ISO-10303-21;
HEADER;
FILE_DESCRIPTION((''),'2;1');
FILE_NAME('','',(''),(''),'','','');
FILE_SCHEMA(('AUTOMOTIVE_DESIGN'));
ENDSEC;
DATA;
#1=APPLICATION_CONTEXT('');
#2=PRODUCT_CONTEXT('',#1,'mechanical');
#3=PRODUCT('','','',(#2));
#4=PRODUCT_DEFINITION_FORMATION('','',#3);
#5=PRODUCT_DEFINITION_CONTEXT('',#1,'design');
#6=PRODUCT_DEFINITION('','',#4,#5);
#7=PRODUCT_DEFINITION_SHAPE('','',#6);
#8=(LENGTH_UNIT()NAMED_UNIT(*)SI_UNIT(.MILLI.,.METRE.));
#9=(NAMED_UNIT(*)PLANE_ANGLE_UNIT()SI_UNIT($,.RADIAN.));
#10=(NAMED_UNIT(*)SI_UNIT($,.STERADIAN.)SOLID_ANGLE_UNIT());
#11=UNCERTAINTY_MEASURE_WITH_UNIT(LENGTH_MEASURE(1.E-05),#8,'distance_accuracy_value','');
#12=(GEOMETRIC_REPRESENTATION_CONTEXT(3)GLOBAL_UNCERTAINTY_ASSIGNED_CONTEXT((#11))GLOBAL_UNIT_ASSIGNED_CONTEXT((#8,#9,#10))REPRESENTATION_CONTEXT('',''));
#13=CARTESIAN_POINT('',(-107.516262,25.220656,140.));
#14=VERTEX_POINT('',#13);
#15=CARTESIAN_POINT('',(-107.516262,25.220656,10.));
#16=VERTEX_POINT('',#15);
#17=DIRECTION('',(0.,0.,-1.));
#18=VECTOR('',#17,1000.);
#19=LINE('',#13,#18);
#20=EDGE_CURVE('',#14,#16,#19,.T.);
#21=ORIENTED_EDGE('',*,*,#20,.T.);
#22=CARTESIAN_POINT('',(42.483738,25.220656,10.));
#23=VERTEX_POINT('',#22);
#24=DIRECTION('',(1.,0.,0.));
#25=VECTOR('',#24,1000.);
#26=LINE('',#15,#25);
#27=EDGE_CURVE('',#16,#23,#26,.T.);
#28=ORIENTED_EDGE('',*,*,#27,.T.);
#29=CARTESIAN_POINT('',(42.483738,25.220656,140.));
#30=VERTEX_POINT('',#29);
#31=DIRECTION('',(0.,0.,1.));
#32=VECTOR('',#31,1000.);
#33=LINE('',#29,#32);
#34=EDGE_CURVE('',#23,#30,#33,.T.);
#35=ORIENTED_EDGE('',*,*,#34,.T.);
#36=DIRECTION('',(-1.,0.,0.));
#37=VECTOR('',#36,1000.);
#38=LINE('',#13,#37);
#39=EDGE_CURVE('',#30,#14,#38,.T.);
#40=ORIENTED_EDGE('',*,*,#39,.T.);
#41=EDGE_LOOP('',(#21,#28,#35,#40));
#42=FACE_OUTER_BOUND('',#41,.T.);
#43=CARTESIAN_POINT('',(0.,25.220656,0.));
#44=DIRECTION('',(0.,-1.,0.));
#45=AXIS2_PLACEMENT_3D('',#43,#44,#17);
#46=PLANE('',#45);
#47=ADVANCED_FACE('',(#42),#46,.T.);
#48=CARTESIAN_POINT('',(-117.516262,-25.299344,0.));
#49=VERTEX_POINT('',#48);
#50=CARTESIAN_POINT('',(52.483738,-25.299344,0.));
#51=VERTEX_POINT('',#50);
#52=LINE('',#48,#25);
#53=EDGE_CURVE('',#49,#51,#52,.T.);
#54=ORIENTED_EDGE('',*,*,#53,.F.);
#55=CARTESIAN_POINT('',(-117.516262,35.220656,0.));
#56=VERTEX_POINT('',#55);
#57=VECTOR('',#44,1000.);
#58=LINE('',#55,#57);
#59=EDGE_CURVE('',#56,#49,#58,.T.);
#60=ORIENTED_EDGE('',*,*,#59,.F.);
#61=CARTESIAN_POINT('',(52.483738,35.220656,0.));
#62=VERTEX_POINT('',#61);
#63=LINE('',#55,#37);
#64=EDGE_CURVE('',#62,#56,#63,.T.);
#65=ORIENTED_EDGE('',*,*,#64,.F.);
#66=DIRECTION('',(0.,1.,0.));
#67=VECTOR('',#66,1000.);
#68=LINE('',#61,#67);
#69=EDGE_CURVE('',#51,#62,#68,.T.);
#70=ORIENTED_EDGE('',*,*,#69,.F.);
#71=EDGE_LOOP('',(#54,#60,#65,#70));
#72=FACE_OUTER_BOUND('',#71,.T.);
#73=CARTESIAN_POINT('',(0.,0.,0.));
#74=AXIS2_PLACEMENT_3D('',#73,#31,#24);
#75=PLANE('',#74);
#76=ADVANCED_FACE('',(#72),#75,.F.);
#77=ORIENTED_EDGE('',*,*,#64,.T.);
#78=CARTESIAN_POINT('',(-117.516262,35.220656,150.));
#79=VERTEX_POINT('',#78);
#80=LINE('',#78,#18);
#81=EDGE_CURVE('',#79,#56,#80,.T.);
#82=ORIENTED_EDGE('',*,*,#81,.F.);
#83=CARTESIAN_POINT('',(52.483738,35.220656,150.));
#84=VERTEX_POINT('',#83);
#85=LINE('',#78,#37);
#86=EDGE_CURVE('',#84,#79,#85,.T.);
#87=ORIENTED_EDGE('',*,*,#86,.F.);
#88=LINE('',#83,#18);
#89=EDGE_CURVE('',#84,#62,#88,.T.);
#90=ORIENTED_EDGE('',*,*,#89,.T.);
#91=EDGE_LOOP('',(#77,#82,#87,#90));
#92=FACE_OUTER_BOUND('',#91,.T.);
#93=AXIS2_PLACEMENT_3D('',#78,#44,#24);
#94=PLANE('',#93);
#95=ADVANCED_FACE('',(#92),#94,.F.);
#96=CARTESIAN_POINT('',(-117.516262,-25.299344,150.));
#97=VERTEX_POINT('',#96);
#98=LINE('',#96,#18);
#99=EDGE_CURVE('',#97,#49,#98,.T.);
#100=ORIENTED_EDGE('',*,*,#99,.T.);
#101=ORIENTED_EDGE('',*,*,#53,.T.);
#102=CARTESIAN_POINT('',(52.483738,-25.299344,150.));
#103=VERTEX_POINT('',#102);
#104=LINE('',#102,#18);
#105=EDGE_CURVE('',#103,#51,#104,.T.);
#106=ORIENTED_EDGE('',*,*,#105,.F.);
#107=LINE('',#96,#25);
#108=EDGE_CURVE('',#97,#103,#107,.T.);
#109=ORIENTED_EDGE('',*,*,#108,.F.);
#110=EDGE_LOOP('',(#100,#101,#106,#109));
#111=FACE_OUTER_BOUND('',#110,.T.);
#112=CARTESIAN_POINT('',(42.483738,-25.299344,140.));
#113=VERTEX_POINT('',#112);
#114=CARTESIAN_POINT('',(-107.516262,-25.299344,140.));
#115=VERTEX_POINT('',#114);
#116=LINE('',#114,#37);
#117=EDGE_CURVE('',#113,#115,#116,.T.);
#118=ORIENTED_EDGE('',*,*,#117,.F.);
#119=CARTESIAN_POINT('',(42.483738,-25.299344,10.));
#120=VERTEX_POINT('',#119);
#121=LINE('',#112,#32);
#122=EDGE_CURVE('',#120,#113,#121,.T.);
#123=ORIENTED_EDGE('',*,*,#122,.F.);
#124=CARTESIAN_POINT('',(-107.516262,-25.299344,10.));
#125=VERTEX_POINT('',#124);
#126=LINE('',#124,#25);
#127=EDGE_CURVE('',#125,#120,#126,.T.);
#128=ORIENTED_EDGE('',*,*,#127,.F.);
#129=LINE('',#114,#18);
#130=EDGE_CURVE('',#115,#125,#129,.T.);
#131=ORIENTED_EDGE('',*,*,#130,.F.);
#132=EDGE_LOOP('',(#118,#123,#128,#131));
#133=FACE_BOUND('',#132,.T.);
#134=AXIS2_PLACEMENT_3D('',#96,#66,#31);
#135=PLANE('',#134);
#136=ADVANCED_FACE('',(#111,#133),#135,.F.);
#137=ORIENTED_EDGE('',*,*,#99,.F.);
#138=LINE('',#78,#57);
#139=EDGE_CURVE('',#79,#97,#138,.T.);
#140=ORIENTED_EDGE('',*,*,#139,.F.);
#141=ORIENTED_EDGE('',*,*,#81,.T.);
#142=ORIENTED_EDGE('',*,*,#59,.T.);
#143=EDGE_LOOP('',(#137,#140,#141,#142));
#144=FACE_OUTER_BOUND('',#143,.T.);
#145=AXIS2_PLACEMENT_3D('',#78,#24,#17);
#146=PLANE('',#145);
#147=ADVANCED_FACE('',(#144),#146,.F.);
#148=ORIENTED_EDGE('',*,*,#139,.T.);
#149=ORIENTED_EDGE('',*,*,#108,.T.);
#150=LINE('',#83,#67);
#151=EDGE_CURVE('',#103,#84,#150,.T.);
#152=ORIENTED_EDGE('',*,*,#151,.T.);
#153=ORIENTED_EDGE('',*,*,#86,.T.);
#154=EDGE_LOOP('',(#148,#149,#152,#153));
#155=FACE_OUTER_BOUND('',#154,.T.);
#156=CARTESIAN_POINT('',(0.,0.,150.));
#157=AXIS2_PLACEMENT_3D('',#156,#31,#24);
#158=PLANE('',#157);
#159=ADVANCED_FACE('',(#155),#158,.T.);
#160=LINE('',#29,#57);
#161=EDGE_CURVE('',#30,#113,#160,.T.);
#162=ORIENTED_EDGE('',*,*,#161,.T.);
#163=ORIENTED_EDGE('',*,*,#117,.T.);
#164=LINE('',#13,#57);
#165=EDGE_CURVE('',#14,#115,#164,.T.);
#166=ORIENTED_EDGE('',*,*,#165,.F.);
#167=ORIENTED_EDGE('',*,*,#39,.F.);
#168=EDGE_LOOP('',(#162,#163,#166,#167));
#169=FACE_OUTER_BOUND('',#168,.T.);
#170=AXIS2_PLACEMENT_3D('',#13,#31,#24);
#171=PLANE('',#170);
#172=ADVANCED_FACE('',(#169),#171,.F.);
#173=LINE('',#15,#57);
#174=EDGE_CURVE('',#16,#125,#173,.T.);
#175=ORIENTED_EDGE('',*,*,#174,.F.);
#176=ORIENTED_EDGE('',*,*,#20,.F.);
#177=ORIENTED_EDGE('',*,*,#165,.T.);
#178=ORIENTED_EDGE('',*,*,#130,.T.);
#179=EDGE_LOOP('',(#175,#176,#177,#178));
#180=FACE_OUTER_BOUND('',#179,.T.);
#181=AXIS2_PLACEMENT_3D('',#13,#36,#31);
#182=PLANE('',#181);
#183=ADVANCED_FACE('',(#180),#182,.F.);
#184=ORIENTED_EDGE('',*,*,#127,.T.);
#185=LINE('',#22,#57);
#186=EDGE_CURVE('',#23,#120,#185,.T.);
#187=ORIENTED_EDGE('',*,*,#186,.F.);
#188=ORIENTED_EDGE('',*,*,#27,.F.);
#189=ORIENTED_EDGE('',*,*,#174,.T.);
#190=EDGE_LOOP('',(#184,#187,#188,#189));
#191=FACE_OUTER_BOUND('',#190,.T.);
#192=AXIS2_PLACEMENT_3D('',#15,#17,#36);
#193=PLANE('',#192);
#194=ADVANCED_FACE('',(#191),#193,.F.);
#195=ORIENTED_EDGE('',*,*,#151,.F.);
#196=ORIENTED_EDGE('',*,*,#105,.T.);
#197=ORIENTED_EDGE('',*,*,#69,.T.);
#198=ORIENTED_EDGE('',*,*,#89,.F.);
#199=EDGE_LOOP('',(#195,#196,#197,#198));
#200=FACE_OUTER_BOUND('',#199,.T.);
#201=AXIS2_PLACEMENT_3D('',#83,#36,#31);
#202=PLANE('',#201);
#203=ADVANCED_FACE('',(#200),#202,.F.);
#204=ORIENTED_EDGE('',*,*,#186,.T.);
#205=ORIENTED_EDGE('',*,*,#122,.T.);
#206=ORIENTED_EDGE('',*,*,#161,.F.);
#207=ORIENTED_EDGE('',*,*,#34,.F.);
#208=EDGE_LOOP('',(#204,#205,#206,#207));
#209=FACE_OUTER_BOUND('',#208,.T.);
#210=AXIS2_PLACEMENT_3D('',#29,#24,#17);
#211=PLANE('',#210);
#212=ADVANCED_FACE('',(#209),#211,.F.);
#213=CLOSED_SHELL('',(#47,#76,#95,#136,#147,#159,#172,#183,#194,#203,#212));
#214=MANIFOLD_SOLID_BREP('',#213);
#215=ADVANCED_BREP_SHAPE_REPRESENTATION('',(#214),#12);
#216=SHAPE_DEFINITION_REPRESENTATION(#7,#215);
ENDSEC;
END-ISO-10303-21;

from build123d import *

# Parameters (mm, degrees)
SKETCH_1_W          = 170
SKETCH_1_H          = 60.52
EXTRUDE_1_DEPTH     = 150
SKETCH_2_W          = 150
SKETCH_2_H          = 130
CUT_EXTRUDE_1_DEPTH = 50.52


with BuildPart() as part:
    # 草图1 → 凸台-拉伸1 (new body)
    with BuildSketch(Plane.XY):
        with Locations((-32.516262295, 4.960655738)):
            Rectangle(SKETCH_1_W, SKETCH_1_H)
    extrude(amount=EXTRUDE_1_DEPTH)

    # 草图2 → 切除-拉伸1 (cut)
    with BuildSketch(Plane.XZ.offset(25.299344262)):
        with Locations((-32.516262295, 75)):
            Rectangle(SKETCH_2_W, SKETCH_2_H)
    extrude(amount=-CUT_EXTRUDE_1_DEPTH, mode=Mode.SUBTRACT)


solid = part.part
